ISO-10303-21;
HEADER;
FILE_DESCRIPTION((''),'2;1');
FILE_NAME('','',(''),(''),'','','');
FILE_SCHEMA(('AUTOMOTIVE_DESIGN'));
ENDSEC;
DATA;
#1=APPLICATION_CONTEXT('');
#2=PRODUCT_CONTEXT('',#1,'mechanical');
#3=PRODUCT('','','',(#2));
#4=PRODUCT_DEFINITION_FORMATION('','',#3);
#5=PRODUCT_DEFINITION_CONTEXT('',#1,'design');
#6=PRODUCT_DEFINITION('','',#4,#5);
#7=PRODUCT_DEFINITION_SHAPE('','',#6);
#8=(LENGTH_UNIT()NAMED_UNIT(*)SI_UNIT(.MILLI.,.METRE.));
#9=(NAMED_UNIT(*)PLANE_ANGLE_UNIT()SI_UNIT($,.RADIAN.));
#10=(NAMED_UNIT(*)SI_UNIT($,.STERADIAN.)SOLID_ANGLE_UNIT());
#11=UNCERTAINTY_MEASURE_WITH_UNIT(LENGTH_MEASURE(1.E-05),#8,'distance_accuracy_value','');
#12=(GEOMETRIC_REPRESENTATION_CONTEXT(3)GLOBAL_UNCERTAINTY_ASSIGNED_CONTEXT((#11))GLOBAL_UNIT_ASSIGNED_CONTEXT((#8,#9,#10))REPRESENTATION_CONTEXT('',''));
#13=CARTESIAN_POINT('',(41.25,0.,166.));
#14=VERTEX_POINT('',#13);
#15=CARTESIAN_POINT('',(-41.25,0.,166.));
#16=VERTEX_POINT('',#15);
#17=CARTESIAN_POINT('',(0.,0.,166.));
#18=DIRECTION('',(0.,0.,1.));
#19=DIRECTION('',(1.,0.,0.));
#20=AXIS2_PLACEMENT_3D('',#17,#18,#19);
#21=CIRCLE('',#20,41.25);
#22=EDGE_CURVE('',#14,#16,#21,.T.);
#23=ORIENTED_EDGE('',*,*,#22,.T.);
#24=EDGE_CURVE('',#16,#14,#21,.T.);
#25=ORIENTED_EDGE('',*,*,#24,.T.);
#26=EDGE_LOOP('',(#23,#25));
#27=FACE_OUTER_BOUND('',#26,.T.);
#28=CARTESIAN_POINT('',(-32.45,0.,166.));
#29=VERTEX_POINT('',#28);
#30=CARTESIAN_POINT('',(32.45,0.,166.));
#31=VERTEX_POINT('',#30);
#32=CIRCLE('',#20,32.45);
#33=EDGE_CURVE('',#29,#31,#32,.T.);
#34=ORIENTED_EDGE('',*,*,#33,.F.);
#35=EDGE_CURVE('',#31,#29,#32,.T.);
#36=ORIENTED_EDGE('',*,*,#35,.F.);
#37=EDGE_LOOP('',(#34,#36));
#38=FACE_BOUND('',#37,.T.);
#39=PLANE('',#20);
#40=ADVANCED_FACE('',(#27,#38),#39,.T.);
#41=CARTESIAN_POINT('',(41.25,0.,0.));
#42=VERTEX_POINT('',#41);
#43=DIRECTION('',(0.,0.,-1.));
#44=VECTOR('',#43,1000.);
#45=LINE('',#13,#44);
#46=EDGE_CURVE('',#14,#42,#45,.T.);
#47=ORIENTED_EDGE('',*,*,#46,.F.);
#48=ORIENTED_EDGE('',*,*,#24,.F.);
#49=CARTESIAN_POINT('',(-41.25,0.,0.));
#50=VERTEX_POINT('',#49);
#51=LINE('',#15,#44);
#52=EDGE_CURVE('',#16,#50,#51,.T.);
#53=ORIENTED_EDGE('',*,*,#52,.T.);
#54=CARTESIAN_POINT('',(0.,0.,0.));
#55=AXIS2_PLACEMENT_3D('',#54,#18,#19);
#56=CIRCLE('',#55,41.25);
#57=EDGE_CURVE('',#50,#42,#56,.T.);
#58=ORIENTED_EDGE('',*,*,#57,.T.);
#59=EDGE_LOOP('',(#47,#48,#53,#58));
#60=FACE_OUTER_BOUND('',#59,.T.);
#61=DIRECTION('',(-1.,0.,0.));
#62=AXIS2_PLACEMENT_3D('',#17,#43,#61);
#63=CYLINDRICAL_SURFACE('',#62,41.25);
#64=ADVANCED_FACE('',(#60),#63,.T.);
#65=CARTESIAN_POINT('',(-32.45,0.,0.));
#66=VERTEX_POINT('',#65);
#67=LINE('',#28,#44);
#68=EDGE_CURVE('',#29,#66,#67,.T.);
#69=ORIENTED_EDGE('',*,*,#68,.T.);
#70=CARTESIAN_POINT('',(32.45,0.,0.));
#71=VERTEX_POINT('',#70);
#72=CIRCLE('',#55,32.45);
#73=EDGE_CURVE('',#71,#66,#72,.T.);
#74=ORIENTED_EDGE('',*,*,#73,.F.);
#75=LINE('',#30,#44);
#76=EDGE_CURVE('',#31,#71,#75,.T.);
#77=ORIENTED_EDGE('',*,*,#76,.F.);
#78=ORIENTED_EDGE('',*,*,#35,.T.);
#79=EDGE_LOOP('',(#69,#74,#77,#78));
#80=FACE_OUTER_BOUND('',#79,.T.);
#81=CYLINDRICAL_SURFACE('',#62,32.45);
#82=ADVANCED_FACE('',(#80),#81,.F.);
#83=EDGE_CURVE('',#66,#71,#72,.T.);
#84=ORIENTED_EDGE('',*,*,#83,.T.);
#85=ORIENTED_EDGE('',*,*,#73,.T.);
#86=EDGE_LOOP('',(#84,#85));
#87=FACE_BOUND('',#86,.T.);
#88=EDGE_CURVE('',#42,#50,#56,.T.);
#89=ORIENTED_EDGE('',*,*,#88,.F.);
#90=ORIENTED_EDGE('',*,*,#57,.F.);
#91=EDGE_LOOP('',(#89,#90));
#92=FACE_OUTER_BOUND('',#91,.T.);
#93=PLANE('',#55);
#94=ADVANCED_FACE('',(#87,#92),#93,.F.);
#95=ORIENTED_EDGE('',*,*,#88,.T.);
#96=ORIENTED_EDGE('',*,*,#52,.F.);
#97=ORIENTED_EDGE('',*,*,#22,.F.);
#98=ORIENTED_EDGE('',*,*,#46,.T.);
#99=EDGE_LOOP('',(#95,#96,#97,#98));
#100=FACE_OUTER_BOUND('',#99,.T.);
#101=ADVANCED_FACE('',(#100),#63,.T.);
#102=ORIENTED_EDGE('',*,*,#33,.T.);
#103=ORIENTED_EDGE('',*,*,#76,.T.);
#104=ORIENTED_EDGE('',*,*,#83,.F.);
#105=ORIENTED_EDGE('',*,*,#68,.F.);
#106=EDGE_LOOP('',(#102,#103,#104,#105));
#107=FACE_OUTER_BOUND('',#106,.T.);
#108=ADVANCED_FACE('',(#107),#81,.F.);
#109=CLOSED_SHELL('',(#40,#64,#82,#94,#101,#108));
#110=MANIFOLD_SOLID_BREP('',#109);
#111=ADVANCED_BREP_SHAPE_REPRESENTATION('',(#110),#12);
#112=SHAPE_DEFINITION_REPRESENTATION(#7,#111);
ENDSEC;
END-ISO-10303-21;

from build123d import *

# Parameters (mm, degrees)
SKETCH1_R           = 41.25
SKETCH1_R_2         = 32.45
BOSS_EXTRUDE1_DEPTH = 166


with BuildPart() as part:
    # Sketch1 → Boss-Extrude1 (new body)
    with BuildSketch(Plane.XY):
        Circle(SKETCH1_R)
        Circle(SKETCH1_R_2, mode=Mode.SUBTRACT)
    extrude(amount=BOSS_EXTRUDE1_DEPTH)


solid = part.part
